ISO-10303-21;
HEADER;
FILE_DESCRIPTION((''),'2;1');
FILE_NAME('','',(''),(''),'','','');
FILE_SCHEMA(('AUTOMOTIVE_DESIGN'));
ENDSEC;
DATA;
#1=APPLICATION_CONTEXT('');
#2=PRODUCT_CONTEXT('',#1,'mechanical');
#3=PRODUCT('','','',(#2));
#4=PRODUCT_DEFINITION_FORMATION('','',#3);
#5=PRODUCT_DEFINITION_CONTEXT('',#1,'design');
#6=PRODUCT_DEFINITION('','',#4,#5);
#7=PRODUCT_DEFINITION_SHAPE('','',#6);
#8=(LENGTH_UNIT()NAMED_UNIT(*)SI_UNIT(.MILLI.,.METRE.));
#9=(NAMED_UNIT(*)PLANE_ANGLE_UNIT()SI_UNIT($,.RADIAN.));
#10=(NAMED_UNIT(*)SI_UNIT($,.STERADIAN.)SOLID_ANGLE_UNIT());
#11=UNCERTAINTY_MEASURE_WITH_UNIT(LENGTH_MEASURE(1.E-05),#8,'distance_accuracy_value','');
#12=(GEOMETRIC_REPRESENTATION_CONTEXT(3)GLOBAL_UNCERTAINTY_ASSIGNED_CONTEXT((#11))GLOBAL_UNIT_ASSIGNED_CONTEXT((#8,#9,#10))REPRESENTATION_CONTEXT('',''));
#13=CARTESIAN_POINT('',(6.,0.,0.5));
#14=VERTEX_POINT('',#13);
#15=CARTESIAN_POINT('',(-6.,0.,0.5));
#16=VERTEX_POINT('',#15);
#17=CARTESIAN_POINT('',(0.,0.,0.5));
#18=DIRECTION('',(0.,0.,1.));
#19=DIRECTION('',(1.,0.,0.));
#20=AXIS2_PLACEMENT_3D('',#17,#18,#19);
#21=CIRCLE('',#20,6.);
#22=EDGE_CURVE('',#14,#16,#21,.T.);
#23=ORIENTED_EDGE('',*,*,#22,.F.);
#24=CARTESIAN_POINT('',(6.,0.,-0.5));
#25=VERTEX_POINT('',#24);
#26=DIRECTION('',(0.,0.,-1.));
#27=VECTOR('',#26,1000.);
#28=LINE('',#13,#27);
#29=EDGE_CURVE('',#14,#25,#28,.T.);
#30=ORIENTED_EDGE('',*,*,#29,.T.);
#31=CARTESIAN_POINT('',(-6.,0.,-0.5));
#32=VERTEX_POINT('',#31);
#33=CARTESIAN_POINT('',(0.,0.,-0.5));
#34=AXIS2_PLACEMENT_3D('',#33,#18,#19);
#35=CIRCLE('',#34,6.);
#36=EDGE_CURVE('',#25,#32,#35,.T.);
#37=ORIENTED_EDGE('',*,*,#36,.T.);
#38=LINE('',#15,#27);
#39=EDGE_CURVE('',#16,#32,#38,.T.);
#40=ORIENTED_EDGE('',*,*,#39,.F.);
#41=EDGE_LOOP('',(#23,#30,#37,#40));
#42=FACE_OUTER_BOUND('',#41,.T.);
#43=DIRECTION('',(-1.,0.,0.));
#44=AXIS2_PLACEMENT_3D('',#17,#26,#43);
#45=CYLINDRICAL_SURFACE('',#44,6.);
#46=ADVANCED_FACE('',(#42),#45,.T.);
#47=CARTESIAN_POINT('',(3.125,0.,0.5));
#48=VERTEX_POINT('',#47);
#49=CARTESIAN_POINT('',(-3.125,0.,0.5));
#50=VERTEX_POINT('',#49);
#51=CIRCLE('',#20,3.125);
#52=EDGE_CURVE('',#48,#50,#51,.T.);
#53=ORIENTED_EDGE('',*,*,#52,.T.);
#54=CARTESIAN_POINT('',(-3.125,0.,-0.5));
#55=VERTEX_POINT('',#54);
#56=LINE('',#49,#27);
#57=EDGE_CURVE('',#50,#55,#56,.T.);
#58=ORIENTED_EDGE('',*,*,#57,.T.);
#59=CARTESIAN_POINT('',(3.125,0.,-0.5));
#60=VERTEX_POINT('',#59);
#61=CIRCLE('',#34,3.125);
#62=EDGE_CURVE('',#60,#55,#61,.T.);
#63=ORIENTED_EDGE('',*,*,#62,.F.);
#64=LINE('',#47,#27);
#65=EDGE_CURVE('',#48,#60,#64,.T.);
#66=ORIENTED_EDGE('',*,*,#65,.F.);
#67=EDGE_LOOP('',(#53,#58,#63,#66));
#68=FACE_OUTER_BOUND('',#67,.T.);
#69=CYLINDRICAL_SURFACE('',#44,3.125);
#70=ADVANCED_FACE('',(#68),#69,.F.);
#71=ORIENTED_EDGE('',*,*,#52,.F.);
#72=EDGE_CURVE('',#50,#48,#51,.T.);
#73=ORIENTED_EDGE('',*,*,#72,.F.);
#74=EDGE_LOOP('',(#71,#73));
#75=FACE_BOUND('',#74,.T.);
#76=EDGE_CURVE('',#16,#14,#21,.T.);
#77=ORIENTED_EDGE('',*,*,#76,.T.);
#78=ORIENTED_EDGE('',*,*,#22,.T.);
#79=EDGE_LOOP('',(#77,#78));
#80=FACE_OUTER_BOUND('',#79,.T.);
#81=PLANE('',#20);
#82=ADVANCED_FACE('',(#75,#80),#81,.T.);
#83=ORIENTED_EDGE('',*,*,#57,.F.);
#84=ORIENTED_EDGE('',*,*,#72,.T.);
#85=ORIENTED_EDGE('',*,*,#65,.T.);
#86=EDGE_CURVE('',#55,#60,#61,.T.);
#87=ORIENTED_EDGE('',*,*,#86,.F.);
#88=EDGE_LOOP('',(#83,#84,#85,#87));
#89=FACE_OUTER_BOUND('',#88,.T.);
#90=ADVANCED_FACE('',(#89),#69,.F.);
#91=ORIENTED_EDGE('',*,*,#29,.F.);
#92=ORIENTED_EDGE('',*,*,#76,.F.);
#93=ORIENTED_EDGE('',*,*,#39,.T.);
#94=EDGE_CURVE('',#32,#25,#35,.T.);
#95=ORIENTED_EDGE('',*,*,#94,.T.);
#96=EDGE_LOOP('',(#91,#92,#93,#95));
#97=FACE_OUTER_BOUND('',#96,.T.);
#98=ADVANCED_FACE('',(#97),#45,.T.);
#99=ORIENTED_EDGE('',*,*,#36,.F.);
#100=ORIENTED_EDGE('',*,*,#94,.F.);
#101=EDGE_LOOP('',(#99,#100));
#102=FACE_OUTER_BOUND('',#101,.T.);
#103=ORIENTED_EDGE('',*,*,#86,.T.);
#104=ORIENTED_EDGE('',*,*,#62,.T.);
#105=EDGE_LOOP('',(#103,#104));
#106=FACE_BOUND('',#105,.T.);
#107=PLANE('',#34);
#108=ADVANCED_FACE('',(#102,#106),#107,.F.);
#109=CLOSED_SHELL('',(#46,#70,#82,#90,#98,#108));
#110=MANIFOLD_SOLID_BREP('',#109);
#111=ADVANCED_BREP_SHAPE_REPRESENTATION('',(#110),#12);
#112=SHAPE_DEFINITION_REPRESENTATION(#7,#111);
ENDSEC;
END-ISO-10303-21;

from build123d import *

# Parameters (mm, degrees)
WASHER_PROFILE_12_X_6_25_R   = 6
WASHER_PROFILE_12_X_6_25_R_2 = 3.125
WASHER_BODY_1MM_DEPTH        = 0.5


with BuildPart() as part:
    # Washer Profile Ø12 x Ø6.25 → Washer Body 1mm (new, symmetric)
    with BuildSketch(Plane.XY):
        Circle(WASHER_PROFILE_12_X_6_25_R)
        Circle(WASHER_PROFILE_12_X_6_25_R_2, mode=Mode.SUBTRACT)
    extrude(amount=WASHER_BODY_1MM_DEPTH, both=True)


solid = part.part
